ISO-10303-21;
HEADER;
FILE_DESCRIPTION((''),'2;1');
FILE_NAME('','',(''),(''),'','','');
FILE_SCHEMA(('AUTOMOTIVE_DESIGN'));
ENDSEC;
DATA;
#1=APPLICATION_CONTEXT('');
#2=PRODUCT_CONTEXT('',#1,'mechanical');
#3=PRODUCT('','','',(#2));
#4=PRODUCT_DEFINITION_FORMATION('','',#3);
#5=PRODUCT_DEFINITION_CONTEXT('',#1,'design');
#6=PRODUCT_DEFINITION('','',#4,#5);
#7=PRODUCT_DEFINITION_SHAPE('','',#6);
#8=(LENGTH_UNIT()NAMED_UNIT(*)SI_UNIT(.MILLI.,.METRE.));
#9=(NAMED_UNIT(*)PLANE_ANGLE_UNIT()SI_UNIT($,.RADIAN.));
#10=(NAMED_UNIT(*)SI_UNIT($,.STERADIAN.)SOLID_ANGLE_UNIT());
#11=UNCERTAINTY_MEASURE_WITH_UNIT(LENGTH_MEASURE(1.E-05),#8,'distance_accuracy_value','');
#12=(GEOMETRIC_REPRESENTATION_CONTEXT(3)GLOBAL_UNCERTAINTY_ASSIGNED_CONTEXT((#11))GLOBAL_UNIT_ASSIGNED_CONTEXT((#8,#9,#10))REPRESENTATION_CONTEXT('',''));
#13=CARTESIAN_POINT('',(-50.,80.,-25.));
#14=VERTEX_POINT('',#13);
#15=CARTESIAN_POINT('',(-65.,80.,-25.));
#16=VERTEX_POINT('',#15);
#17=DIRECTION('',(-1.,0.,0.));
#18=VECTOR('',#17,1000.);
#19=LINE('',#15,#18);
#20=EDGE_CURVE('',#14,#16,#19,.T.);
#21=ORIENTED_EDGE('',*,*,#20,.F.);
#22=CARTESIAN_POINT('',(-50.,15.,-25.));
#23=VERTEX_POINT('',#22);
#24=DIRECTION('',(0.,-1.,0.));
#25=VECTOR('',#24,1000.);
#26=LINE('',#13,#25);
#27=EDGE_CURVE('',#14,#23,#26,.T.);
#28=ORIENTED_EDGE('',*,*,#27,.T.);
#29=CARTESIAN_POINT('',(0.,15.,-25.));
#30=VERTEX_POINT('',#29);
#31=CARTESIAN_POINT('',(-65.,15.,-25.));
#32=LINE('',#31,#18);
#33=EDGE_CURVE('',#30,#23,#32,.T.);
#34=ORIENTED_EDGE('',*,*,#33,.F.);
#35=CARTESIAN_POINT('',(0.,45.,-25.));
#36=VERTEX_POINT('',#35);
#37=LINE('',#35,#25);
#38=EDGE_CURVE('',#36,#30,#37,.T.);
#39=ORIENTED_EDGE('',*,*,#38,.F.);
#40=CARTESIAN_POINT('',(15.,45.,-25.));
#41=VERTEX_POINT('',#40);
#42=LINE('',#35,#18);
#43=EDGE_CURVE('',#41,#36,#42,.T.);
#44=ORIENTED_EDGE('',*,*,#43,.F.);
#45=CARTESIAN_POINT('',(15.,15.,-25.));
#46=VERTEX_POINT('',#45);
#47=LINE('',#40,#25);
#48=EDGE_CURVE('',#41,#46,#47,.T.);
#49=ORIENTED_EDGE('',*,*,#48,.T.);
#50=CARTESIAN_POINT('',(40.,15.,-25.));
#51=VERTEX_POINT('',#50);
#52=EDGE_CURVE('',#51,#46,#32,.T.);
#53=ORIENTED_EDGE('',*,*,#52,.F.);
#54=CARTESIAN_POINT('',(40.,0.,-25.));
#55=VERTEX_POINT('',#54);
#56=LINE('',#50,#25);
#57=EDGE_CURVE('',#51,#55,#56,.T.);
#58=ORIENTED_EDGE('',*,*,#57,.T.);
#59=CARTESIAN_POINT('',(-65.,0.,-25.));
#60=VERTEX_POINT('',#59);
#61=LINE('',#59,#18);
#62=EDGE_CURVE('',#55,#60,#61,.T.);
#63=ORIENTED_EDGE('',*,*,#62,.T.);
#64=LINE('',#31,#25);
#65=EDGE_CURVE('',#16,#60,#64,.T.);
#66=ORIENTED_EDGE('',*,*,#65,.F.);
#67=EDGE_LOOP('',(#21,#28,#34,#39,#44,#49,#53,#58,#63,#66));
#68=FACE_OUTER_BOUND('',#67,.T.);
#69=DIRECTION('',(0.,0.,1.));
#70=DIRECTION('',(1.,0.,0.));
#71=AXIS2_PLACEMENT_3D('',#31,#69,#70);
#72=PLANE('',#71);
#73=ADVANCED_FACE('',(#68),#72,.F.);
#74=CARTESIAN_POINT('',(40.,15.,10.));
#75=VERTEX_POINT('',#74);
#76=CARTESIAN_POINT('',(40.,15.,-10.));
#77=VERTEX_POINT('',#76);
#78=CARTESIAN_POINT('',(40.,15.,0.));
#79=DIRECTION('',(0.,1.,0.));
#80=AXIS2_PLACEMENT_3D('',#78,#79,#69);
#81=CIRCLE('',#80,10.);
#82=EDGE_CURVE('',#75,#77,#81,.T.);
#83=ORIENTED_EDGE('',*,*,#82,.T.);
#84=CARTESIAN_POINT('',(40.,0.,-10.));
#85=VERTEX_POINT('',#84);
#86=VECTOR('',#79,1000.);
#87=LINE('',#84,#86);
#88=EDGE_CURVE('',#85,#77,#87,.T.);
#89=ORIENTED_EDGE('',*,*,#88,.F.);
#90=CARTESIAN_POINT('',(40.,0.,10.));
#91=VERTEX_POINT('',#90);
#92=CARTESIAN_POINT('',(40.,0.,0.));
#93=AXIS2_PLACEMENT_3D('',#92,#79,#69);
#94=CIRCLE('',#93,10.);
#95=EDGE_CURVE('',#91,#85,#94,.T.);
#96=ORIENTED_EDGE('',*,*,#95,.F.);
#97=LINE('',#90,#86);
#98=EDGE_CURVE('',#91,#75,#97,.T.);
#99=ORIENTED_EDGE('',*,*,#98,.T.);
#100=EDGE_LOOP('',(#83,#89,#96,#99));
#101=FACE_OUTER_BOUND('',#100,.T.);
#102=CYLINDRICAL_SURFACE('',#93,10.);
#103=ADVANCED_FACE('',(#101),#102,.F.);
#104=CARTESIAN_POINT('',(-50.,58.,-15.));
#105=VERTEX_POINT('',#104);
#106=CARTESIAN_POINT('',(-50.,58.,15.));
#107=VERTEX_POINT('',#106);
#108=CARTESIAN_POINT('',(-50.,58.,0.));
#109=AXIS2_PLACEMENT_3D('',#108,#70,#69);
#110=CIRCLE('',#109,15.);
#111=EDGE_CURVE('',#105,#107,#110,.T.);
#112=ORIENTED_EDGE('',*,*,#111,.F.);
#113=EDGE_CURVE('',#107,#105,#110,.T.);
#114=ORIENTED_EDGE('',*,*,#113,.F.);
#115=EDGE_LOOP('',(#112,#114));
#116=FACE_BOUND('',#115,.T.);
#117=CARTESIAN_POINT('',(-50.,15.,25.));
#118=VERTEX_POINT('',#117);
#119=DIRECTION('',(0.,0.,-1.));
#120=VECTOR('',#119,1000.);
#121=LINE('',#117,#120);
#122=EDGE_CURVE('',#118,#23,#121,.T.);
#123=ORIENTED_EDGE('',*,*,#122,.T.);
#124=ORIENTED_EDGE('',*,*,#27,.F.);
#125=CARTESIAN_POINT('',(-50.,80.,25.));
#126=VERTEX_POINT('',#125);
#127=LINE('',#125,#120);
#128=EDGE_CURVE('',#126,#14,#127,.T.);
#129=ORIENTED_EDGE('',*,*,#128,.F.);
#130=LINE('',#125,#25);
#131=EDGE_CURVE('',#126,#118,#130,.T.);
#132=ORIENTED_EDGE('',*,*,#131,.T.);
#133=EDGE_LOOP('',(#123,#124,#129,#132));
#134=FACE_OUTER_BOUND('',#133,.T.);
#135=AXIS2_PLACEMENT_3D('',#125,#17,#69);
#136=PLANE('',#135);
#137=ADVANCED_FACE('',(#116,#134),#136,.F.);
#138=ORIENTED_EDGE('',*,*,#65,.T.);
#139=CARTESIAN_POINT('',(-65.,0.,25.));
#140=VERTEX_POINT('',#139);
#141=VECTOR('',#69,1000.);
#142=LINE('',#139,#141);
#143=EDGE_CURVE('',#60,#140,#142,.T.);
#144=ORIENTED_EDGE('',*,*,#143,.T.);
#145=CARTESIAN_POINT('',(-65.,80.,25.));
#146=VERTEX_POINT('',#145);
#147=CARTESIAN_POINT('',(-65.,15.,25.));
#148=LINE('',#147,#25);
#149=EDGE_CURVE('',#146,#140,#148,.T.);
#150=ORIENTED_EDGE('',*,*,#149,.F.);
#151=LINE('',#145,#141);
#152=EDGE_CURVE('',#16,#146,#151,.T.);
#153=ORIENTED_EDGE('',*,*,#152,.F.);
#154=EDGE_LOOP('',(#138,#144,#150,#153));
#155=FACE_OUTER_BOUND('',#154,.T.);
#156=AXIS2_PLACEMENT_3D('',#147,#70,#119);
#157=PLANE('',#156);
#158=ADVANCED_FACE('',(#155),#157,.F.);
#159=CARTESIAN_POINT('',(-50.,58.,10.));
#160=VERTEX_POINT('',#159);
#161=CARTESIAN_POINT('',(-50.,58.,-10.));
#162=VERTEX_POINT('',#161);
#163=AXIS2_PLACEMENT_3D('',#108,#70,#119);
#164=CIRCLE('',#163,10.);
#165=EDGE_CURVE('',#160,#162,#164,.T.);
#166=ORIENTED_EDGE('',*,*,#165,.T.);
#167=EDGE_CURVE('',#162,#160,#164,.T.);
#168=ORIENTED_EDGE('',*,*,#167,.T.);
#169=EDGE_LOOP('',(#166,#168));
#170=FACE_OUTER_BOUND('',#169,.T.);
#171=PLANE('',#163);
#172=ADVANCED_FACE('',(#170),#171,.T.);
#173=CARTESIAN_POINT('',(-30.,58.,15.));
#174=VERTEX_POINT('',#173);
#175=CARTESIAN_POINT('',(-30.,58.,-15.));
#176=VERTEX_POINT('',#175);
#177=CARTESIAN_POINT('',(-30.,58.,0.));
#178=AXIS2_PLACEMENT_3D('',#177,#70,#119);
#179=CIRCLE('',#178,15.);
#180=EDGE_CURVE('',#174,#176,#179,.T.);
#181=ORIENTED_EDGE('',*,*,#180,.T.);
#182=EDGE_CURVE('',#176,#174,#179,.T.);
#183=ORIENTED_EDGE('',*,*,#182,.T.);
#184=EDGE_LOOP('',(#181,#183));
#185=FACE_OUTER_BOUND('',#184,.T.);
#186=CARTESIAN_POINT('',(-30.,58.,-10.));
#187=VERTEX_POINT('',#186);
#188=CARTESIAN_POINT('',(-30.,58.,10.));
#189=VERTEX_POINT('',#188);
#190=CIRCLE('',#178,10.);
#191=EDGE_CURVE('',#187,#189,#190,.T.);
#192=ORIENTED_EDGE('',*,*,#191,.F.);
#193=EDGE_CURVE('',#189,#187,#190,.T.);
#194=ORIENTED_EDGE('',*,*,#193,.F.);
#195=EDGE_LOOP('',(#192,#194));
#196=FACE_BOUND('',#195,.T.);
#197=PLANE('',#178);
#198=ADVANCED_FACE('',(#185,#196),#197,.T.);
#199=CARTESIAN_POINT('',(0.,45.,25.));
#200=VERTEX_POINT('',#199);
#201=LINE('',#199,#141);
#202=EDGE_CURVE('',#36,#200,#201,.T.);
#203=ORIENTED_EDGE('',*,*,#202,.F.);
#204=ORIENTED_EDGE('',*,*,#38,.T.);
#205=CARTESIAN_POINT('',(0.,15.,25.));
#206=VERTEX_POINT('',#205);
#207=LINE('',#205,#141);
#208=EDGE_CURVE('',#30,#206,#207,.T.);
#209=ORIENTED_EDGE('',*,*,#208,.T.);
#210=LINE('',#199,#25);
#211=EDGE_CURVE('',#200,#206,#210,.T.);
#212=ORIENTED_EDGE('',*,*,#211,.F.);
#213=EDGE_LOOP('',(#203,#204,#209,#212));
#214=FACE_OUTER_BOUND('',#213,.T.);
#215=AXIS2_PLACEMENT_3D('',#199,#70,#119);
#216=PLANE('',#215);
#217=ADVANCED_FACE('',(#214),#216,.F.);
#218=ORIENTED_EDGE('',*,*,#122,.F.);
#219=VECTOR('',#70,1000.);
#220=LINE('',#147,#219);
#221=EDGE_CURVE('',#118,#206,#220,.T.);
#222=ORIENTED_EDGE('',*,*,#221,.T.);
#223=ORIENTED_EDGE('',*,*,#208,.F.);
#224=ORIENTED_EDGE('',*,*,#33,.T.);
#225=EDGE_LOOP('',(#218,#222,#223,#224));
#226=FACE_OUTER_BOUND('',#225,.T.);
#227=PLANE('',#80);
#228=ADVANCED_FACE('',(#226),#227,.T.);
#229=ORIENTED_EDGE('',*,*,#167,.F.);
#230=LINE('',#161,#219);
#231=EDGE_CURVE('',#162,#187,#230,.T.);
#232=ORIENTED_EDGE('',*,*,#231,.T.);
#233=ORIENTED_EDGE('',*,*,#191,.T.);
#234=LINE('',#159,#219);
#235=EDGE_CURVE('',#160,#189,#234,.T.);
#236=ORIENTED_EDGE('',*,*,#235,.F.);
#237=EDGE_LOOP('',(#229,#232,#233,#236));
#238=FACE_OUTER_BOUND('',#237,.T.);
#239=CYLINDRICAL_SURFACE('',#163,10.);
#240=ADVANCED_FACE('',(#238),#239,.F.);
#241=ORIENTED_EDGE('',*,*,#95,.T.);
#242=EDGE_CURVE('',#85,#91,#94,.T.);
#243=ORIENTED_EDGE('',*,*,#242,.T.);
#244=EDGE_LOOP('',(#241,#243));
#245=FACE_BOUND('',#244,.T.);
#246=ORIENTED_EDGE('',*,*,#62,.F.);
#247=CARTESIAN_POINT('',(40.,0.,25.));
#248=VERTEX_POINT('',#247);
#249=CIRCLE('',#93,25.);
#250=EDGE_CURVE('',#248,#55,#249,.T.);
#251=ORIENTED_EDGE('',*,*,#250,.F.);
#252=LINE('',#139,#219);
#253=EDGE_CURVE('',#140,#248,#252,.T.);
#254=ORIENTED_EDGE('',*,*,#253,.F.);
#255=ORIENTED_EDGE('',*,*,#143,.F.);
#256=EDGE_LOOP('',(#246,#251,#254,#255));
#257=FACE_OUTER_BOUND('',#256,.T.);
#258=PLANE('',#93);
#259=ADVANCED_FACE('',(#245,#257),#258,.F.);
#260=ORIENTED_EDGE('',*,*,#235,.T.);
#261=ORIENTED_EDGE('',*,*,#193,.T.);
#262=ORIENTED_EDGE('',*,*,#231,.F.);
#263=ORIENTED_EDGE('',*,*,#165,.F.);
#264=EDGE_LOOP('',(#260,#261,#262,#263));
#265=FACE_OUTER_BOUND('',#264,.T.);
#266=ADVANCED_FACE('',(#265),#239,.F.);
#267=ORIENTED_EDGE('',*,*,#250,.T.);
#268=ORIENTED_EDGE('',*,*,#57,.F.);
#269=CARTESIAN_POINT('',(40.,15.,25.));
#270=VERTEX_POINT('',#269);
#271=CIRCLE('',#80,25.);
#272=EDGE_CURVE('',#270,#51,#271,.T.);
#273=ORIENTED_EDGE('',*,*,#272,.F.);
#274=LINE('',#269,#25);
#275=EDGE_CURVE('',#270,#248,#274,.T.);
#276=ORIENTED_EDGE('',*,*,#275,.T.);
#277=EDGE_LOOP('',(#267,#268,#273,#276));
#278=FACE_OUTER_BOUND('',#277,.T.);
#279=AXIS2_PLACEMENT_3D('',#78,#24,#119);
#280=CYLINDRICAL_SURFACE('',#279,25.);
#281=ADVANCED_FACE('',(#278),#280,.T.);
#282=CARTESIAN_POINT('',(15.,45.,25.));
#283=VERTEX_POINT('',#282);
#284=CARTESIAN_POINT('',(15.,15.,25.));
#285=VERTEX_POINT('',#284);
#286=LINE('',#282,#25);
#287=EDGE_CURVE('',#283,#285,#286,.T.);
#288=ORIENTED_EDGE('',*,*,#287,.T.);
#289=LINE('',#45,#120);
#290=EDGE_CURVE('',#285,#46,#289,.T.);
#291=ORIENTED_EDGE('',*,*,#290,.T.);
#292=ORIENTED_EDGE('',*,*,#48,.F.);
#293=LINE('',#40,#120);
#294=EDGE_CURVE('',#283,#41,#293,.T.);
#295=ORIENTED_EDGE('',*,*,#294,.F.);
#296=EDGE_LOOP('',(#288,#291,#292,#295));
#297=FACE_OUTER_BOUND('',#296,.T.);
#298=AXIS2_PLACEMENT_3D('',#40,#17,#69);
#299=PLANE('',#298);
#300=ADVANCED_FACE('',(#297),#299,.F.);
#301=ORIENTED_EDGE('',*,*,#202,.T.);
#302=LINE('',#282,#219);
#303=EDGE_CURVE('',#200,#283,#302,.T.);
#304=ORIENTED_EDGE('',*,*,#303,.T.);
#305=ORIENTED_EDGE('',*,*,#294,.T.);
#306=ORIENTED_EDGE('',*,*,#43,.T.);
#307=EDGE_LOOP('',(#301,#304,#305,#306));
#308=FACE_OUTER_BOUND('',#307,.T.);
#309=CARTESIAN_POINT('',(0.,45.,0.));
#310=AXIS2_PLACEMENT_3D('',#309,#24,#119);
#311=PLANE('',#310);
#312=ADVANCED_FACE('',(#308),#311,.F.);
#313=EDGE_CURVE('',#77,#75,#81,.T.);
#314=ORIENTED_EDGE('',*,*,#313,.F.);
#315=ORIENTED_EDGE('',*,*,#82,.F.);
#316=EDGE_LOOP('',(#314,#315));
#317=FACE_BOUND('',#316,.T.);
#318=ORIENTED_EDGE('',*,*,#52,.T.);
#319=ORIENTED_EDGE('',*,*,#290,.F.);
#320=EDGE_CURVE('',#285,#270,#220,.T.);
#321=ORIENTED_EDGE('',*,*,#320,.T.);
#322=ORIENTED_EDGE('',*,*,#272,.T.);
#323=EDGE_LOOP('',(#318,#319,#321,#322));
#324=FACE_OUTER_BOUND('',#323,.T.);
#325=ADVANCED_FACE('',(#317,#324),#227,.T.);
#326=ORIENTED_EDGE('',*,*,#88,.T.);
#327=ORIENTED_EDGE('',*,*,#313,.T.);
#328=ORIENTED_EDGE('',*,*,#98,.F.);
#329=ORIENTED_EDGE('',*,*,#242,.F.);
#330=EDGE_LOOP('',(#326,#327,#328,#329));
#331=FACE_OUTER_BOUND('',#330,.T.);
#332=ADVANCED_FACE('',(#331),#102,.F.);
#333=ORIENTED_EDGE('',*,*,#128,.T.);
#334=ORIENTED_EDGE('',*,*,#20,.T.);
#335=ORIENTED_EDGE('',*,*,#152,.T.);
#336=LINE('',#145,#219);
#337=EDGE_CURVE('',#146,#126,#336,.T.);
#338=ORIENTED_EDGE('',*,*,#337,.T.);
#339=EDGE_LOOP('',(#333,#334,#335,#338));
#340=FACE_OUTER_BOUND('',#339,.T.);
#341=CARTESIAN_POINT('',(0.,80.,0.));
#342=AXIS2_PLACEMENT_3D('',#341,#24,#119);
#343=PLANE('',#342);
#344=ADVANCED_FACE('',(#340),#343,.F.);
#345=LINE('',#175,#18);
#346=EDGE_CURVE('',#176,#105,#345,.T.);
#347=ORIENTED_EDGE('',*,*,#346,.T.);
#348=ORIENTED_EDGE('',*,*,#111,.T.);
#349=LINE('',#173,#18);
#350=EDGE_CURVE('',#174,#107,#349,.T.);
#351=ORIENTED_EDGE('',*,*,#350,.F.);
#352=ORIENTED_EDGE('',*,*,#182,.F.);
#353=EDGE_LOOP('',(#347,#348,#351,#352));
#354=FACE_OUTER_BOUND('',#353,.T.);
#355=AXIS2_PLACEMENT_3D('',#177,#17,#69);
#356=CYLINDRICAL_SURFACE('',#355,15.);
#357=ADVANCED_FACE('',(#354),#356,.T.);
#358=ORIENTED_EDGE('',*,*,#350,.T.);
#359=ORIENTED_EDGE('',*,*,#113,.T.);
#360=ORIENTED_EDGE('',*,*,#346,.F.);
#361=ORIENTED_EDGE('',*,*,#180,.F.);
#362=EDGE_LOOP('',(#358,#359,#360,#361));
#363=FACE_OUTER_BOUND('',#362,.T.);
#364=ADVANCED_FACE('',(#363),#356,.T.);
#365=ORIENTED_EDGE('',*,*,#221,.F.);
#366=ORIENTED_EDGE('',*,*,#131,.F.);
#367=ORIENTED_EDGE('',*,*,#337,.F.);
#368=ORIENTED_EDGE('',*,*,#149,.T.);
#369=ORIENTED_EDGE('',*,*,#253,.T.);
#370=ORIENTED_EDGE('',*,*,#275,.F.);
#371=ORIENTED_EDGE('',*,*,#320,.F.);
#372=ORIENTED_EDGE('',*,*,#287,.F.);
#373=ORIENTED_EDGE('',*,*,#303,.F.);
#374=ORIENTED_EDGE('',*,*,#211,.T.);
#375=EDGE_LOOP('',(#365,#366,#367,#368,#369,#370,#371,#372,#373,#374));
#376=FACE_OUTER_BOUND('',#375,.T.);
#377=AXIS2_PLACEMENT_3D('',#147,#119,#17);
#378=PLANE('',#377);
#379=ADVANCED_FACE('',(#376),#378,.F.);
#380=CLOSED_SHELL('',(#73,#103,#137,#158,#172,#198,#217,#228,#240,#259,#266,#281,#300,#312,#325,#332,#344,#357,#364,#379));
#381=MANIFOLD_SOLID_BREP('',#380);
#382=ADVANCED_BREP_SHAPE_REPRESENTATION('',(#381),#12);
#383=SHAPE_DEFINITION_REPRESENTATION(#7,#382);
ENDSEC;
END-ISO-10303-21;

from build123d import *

# Parameters (mm, degrees)
BASE_PLATE_DEPTH      = 15
UPRIGHT_WALL_SKETCH_W = 15
UPRIGHT_WALL_SKETCH_H = 50
UPRIGHT_WALL_DEPTH    = 65
WALL_BOSS_SKETCH_R    = 15
WALL_BOSS_DEPTH       = 20
BOSS_BORE_SKETCH_R    = 10
BOSS_BORE_10_DEPTH    = 20
RAISED_BLOCK_SKETCH_W = 15
RAISED_BLOCK_SKETCH_H = 50
RAISED_BLOCK_DEPTH    = 30
LUG_HOLE_SKETCH_R     = 10
LUG_HOLE_DEPTH        = 15


with BuildPart() as part:
    # Base Plate Sketch → Base Plate (new body)
    with BuildSketch(Plane(origin=(0, 0, 0), x_dir=(1, 0, 0), z_dir=(0, 1, 0))):
        with BuildLine():
            Line((-65, -25), (40, -25))
            ThreePointArc((40, -25), (65, 0), (40, 25))
            Line((40, 25), (-65, 25))
            Line((-65, 25), (-65, -25))
        make_face()
    extrude(amount=BASE_PLATE_DEPTH)

    # Upright Wall Sketch → Upright Wall (add)
    with BuildSketch(Plane(origin=(0, 15, 0), x_dir=(1, 0, 0), z_dir=(0, 1, 0))):
        with Locations((-57.5, 0)):
            Rectangle(UPRIGHT_WALL_SKETCH_W, UPRIGHT_WALL_SKETCH_H)
    extrude(amount=UPRIGHT_WALL_DEPTH)

    # Wall Boss Sketch → Wall Boss (add)
    with BuildSketch(Plane(origin=(-50, 0, 0), x_dir=(0, 0, -1), z_dir=(1, 0, 0))):
        with Locations(Location((0, 58, 0), (0, 0, 180))):
            Circle(WALL_BOSS_SKETCH_R)
    extrude(amount=WALL_BOSS_DEPTH)

    # Boss Bore Sketch → Boss Bore Ø10 (cut)
    with BuildSketch(Plane(origin=(-30, 0, 0), x_dir=(0, 0, -1), z_dir=(1, 0, 0))):
        with Locations((0, 58)):
            Circle(BOSS_BORE_SKETCH_R)
    extrude(amount=-BOSS_BORE_10_DEPTH, mode=Mode.SUBTRACT)

    # Raised Block Sketch → Raised Block (add)
    with BuildSketch(Plane(origin=(0, 15, 0), x_dir=(1, 0, 0), z_dir=(0, 1, 0))):
        with Locations((7.5, 0)):
            Rectangle(RAISED_BLOCK_SKETCH_W, RAISED_BLOCK_SKETCH_H)
    extrude(amount=RAISED_BLOCK_DEPTH)

    # Lug Hole Sketch → Lug Hole (cut)
    with BuildSketch(Plane(origin=(0, 15, 0), x_dir=(1, 0, 0), z_dir=(0, 1, 0))):
        with Locations(Location((40, 0, 0), (0, 0, 270))):
            Circle(LUG_HOLE_SKETCH_R)
    extrude(amount=-LUG_HOLE_DEPTH, mode=Mode.SUBTRACT)


solid = part.part
